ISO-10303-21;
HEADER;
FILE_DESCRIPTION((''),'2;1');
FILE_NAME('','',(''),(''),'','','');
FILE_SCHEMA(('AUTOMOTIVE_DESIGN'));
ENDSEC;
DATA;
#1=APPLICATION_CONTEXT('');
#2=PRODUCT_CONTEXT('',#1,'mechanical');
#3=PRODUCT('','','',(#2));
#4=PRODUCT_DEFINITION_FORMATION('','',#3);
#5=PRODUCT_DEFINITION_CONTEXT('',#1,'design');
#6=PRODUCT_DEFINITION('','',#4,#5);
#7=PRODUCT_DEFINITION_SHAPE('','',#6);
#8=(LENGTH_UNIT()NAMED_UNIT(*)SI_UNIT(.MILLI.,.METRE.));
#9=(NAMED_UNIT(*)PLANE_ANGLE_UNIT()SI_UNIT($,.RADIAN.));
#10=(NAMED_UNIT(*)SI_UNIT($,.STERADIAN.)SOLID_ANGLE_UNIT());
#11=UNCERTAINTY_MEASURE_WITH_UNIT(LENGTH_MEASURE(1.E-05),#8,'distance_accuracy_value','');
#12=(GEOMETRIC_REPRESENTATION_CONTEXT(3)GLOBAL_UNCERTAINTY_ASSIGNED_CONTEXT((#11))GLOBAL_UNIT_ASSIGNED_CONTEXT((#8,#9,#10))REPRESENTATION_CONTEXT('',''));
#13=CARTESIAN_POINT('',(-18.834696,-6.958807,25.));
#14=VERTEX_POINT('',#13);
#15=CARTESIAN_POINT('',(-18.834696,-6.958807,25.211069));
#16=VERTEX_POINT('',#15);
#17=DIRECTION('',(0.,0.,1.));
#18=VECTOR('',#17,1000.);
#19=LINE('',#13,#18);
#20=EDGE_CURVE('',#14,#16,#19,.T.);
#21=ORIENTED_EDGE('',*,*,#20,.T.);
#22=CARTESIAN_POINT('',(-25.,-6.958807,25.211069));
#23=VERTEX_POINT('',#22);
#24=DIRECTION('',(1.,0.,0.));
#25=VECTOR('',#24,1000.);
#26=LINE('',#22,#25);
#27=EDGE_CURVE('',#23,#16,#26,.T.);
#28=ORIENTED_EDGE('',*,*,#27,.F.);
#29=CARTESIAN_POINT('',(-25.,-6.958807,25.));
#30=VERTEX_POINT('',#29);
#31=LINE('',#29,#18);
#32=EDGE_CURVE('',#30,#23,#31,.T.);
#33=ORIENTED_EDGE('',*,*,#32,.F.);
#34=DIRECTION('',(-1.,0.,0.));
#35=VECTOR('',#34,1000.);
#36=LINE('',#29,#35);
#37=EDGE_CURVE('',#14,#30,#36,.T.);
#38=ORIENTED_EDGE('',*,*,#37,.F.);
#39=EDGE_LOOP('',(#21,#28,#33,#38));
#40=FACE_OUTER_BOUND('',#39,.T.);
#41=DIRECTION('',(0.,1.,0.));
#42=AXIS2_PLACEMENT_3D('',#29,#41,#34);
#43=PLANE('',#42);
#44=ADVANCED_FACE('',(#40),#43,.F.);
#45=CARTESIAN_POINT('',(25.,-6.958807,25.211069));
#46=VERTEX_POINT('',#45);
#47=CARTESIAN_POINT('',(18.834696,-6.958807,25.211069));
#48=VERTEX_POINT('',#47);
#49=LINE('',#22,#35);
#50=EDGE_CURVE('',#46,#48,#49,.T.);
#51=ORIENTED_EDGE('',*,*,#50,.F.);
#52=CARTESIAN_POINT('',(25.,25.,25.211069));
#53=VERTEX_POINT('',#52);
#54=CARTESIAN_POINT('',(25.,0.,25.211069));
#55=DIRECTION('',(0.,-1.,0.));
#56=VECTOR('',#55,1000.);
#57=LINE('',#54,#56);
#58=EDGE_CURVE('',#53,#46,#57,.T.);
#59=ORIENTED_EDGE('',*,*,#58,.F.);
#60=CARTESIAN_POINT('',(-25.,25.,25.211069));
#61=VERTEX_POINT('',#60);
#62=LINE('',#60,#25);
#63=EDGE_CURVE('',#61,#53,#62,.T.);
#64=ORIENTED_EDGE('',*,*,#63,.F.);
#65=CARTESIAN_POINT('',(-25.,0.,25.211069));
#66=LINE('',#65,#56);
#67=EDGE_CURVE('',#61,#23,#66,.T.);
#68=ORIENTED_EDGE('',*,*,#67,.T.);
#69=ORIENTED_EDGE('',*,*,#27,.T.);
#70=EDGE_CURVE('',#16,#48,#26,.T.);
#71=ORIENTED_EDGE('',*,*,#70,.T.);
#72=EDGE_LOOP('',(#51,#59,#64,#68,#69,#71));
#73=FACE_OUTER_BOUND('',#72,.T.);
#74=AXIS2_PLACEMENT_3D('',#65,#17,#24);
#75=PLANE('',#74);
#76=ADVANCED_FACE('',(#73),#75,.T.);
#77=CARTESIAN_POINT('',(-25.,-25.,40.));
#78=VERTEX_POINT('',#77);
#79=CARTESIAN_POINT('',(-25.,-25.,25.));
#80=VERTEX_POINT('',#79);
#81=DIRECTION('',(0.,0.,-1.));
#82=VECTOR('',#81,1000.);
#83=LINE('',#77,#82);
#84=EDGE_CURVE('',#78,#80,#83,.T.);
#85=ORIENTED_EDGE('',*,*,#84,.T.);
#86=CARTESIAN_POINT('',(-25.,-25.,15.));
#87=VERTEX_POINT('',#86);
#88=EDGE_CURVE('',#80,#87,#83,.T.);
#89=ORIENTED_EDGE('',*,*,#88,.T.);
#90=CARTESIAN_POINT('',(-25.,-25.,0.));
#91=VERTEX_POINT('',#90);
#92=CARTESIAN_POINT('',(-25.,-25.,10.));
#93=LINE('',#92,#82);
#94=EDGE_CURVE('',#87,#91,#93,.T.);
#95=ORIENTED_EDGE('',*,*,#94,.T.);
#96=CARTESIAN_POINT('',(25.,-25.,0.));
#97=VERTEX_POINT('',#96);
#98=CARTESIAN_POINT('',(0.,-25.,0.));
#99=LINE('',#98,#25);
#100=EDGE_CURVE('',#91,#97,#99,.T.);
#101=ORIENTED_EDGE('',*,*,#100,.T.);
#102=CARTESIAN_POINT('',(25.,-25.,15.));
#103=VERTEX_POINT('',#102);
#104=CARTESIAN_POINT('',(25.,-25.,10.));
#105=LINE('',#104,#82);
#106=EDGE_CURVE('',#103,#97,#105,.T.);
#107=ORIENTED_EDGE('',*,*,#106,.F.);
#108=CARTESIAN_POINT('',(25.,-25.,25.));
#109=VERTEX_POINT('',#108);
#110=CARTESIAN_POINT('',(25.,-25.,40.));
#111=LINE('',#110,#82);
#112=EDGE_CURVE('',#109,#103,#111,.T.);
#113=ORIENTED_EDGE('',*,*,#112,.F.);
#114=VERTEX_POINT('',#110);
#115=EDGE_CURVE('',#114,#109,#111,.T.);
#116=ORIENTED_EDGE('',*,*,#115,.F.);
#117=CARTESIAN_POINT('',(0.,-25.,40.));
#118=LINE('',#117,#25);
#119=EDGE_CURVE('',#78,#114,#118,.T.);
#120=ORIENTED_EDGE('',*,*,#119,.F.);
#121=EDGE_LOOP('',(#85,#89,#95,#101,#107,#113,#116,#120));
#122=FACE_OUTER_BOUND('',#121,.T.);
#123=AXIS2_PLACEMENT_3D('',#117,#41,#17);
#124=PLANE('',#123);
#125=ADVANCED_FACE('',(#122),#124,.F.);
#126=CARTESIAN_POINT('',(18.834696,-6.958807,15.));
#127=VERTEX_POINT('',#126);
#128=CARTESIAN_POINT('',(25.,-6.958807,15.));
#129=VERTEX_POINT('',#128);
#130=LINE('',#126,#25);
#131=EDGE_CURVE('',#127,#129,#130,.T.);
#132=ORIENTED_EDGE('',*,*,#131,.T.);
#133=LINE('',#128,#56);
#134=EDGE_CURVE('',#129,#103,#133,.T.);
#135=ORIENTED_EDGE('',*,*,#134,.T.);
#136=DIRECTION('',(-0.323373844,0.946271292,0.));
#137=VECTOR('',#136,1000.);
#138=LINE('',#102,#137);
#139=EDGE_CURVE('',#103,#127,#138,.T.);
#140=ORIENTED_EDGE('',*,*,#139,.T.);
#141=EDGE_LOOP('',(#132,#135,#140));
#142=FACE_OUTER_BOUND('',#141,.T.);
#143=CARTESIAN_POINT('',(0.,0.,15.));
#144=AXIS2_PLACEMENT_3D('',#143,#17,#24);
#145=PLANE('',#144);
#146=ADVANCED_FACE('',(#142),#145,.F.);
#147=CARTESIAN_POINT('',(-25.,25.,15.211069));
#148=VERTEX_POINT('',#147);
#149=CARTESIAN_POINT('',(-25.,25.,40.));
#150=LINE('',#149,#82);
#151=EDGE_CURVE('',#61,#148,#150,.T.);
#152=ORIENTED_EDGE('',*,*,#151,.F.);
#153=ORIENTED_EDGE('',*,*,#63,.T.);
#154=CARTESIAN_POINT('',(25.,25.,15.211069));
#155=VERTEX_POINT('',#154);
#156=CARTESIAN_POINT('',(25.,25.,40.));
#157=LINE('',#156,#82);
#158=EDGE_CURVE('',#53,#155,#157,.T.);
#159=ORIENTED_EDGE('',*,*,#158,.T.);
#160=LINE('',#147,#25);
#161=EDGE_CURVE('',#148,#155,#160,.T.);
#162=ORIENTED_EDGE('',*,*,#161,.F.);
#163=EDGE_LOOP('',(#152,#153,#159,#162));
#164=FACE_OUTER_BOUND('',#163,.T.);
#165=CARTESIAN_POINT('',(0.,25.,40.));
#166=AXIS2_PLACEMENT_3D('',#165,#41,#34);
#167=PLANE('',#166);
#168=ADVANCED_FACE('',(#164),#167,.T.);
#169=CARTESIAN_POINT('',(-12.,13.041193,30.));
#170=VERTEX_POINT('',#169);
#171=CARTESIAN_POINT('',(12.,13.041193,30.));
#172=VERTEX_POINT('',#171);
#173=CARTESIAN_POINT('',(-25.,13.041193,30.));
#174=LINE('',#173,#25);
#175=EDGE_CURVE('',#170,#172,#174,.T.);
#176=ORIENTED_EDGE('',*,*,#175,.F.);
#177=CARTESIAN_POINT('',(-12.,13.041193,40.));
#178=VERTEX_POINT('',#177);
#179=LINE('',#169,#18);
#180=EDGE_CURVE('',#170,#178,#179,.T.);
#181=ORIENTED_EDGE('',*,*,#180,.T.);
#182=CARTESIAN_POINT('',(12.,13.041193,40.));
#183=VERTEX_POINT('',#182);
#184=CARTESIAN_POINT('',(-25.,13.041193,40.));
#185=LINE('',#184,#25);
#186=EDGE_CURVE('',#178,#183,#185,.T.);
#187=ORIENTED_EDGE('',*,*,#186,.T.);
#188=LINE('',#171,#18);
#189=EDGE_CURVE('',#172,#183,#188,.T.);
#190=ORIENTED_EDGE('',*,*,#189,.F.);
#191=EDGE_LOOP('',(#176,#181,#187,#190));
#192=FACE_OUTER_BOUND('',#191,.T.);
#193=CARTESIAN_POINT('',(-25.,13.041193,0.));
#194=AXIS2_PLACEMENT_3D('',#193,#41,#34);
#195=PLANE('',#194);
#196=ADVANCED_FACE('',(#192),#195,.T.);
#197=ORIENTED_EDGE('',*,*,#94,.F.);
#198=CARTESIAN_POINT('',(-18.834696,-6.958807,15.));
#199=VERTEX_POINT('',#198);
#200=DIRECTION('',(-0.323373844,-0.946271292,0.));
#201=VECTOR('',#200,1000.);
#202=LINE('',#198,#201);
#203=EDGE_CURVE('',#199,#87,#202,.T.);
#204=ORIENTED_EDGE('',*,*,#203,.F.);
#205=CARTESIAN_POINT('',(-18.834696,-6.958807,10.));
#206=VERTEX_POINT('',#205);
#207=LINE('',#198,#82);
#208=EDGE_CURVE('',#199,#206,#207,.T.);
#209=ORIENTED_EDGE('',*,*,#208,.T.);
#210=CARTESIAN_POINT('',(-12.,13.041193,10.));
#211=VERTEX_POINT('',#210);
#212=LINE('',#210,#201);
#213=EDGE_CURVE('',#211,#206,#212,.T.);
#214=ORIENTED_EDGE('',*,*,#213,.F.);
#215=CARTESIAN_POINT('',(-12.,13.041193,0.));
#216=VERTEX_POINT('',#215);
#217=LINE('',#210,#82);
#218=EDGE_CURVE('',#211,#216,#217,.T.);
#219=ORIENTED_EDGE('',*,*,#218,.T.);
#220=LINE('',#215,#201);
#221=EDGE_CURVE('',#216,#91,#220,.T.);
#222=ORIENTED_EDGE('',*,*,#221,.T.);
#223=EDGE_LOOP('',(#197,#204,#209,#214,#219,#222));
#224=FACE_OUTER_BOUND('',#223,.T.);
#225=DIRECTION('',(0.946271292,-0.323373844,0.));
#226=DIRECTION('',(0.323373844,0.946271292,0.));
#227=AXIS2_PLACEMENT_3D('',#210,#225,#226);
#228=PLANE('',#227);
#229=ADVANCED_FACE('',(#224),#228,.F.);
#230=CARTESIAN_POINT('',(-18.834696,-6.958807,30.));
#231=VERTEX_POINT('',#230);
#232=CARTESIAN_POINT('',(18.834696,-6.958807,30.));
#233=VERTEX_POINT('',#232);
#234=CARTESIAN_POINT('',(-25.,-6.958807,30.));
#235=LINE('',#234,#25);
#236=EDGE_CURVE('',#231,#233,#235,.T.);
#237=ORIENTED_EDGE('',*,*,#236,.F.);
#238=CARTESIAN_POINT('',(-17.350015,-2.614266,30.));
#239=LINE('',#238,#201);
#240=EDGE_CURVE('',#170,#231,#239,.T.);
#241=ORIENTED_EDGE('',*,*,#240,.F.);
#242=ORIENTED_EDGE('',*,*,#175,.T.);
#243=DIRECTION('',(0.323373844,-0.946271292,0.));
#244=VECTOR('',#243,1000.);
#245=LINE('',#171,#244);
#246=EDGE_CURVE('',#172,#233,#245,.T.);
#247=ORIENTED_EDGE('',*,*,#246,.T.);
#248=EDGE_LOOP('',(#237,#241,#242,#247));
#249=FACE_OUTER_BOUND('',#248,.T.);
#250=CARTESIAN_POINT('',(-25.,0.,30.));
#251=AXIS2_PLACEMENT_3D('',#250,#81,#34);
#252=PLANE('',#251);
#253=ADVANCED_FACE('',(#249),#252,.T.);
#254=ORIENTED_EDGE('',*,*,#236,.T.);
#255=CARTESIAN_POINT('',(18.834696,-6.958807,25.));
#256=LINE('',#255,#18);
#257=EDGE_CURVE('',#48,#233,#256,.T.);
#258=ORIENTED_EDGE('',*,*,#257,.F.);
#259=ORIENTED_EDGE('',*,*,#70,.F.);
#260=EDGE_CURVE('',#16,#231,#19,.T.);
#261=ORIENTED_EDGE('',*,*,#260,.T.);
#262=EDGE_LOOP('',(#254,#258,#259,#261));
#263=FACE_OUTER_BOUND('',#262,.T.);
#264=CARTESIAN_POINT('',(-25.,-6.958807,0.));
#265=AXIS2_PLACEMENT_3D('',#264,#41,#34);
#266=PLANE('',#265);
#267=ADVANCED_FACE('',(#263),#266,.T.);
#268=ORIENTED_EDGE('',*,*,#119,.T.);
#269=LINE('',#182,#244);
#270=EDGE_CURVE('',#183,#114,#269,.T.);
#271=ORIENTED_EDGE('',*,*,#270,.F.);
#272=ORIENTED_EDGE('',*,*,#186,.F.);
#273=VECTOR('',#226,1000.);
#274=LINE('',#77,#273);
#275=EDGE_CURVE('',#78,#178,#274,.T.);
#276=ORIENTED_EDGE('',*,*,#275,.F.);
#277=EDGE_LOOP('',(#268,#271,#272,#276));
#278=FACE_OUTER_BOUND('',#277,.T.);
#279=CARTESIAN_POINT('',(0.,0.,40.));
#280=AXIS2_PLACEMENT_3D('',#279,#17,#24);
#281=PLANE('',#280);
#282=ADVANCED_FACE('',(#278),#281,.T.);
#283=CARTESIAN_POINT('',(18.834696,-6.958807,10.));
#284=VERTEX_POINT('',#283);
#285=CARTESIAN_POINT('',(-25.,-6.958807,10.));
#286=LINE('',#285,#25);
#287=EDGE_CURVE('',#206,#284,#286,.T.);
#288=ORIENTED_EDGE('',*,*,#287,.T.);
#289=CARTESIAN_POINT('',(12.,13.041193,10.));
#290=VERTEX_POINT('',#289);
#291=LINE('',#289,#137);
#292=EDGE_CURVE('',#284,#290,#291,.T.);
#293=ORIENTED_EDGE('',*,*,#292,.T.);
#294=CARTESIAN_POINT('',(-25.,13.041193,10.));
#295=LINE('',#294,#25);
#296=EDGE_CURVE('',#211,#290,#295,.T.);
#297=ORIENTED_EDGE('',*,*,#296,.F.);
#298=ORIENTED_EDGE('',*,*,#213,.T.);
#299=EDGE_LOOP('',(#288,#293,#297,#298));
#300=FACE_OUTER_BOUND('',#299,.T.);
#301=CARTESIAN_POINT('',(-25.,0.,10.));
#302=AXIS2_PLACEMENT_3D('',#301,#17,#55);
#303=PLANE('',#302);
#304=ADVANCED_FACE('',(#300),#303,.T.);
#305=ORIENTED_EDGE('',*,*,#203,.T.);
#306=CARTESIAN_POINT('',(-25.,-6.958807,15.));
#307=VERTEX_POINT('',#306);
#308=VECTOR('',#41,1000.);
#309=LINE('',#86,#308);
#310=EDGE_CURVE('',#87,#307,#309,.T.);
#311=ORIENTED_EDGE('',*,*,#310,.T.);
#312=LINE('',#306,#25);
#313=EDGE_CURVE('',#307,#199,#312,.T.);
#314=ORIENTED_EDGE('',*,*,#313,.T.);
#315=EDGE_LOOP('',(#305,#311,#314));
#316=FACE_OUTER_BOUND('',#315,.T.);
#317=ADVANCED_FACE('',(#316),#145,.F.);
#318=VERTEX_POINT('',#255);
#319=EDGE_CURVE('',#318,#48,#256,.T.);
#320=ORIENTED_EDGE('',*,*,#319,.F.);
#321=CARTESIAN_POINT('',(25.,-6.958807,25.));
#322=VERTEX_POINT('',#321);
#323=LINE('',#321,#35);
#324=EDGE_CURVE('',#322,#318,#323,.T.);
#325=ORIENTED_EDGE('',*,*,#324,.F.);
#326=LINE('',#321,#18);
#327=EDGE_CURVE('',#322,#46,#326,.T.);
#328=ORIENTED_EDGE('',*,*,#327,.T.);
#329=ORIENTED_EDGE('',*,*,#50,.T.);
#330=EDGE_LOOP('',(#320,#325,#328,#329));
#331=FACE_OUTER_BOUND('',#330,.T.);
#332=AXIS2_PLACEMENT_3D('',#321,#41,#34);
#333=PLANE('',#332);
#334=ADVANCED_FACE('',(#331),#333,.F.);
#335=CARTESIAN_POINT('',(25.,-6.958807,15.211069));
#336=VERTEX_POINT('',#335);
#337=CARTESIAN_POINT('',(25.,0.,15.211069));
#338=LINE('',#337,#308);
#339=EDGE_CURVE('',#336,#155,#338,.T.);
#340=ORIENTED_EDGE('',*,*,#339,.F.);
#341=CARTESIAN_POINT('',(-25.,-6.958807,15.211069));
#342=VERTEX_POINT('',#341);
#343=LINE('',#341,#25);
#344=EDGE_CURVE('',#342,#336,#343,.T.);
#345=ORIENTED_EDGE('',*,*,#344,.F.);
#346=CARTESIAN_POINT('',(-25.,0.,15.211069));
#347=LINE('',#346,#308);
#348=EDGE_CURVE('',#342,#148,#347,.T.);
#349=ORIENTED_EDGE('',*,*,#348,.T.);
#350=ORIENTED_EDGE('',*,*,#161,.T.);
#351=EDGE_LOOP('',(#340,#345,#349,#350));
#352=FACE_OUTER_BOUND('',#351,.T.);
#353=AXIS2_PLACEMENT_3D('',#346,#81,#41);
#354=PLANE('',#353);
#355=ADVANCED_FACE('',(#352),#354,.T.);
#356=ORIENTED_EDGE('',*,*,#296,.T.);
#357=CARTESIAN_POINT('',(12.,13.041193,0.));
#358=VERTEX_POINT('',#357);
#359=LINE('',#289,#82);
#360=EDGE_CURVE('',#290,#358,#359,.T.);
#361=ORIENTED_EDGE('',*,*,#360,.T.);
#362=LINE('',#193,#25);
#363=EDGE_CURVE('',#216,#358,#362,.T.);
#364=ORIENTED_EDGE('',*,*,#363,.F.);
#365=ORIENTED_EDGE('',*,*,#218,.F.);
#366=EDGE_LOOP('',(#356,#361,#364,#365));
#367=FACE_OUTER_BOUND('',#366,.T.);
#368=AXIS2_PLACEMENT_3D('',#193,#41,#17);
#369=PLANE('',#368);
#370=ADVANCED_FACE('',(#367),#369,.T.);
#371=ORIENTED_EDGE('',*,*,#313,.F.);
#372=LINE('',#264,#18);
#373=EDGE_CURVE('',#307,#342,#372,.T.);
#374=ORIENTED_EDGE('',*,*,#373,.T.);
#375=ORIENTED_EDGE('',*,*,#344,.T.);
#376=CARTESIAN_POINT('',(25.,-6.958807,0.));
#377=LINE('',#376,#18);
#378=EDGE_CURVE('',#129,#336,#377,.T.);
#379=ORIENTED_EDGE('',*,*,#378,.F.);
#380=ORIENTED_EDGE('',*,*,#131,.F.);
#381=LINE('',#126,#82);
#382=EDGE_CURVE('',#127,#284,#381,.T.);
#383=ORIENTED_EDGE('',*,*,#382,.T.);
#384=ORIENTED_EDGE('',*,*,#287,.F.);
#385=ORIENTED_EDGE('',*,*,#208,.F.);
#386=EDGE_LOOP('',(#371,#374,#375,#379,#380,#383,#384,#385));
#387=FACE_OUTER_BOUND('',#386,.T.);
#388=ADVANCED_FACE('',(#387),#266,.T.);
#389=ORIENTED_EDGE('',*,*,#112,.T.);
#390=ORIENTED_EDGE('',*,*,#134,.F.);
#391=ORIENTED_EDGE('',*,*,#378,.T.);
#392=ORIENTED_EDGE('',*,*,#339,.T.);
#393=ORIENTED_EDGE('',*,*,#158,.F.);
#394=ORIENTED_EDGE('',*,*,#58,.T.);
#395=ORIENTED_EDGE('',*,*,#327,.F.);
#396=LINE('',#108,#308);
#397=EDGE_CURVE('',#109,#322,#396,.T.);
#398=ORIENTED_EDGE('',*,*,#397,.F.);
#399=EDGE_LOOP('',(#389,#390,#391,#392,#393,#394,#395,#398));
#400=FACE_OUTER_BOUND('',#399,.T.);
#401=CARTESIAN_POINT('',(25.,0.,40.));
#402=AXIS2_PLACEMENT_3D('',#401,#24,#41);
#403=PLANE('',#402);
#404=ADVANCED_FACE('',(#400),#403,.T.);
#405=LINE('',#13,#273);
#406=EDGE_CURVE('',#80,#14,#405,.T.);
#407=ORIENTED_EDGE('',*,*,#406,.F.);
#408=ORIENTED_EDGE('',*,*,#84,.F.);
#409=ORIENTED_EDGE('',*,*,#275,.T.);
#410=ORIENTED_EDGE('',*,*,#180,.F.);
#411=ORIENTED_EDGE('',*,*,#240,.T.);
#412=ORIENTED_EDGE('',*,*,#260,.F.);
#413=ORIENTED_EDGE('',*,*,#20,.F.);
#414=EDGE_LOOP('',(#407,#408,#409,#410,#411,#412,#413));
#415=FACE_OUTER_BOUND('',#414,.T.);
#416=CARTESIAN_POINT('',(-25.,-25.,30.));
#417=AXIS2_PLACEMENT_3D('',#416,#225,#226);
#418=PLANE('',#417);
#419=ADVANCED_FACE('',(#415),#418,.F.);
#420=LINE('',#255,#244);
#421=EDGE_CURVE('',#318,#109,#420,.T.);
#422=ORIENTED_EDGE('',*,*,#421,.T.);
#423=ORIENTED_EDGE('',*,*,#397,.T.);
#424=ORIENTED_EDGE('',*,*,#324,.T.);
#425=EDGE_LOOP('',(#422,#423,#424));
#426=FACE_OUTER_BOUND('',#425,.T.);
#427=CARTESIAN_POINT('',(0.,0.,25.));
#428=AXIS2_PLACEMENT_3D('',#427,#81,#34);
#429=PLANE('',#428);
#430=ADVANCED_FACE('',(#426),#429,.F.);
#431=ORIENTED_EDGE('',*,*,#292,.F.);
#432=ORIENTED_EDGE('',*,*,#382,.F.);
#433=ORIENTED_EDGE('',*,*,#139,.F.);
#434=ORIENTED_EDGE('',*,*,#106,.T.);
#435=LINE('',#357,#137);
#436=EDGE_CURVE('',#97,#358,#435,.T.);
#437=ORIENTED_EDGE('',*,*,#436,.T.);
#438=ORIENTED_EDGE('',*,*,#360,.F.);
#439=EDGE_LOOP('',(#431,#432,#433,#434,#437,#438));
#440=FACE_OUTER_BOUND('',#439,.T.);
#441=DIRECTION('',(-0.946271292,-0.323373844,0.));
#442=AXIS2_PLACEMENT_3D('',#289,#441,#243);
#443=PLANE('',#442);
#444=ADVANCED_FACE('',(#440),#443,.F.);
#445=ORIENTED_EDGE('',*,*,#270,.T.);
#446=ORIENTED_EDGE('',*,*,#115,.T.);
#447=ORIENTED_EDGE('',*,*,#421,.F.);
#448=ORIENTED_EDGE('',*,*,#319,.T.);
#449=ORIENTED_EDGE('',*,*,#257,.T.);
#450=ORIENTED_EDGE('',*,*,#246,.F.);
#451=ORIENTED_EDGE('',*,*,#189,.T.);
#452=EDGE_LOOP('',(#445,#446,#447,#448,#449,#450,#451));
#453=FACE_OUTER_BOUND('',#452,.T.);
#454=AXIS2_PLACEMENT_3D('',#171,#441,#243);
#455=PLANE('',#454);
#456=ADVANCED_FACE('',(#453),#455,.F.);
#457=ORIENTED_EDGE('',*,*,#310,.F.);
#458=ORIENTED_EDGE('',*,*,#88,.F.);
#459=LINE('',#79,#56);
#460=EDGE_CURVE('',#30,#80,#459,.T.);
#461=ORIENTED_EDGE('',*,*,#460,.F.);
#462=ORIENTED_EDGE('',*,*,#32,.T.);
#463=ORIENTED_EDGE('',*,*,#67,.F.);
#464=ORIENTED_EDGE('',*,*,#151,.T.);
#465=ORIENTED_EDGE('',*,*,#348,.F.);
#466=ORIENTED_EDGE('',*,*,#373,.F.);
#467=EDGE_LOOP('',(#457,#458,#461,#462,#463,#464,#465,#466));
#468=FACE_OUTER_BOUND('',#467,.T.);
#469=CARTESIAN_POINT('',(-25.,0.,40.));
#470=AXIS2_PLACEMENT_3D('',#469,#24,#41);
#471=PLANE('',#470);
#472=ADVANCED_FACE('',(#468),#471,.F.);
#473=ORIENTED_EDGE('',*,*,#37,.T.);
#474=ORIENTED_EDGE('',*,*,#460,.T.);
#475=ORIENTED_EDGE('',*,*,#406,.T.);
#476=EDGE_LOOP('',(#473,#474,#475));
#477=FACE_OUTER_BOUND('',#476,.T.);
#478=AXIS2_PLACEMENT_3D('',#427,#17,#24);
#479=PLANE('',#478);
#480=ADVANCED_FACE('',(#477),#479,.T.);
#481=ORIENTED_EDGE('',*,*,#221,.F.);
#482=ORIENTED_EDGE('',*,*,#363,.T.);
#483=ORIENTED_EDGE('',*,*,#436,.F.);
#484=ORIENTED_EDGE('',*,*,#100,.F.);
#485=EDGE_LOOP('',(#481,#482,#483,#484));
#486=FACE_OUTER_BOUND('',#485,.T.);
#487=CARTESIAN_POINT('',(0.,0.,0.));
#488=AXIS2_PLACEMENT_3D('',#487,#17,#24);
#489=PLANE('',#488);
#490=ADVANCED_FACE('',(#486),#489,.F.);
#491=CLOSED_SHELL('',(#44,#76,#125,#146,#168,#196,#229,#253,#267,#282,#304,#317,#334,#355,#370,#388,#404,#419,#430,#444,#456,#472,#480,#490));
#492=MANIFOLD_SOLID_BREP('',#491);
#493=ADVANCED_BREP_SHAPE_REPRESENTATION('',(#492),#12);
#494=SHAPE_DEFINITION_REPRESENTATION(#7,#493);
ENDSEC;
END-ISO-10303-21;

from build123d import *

# Parameters (mm, degrees)
BASE_BLOCK_40MM_DEPTH       = 40
STEP_PROFILE_CUT_SKETCH_W   = 10
STEP_PROFILE_CUT_SKETCH_H   = 11.958807021
STEP_PROFILE_CUT_DEPTH      = 69.738635424
POCKET_24MM_X_10_DEEP_DEPTH = 10
POCKET_12MM_X_10_DEEP_DEPTH = 10
TRIANGULAR_CUT_A_5MM_DEPTH  = 5
TRIANGULAR_CUT_B_5MM_DEPTH  = 5
TRIANGULAR_CUT_C_5MM_DEPTH  = 5
TRIANGULAR_CUT_D_5MM_DEPTH  = 5


with BuildPart() as part:
    # Base Profile Sketch → Base Block 40mm (new body)
    with BuildSketch(Plane.XY):
        Polygon((12, 25), (-12, 25), (-25, 25), (-25, -25), (-12, 13), (12, 13), (25, -25), (25, 25), align=None)
        Polygon((12, 13), (25, -25), (-25, -25), (-12, 13), align=None)
    extrude(amount=BASE_BLOCK_40MM_DEPTH)

    # Step Profile Cut Sketch → Step Profile Cut (cut, through all)
    with BuildSketch(Plane(origin=(25, 0, 0), x_dir=(0, 0, -1), z_dir=(1, 0, 0))):
        Polygon((-25.21106926, -6.958807021), (-25.21106926, 25), (-30, 25), (-40, 25), (-40, 13.041192979), (-30, 13.041192979), (-30, -6.958807021), align=None)
        Polygon((-10, -6.958807021), (-10, 13.041192979), (-10, 25), (-15.21106926, 25), (-15.21106926, -6.958807021), align=None)
        with Locations((-5, 19.02059649)):
            Rectangle(STEP_PROFILE_CUT_SKETCH_W, STEP_PROFILE_CUT_SKETCH_H)
    extrude(amount=-STEP_PROFILE_CUT_DEPTH, mode=Mode.SUBTRACT)

    # Pocket 24mm Sketch → Pocket 24mm x 10 Deep (cut)
    with BuildSketch(Plane(origin=(0, 0, 0), x_dir=(-1, 0, 0), z_dir=(0, 0, -1))):
        Polygon((-12, 13.041192979), (12, 13.041192979), (25, -25), (25, 25), (-25, 25), (-25, -25), align=None)
    extrude(amount=-POCKET_24MM_X_10_DEEP_DEPTH, mode=Mode.SUBTRACT)

    # Pocket 12mm Sketch → Pocket 12mm x 10 Deep (cut)
    with BuildSketch(Plane.XY.offset(40)):
        Polygon((-25, -25), (-12, 13.041192979), (12, 13.041192979), (25, -25), (25, 25), (-25, 25), align=None)
    extrude(amount=-POCKET_12MM_X_10_DEEP_DEPTH, mode=Mode.SUBTRACT)

    # Triangular Cut A Sketch → Triangular Cut A 5mm (cut)
    with BuildSketch(Plane.XY.offset(30)):
        Polygon((-25, -25), (-25, -6.958807021), (-18.834696276, -6.958807021), align=None)
    extrude(amount=-TRIANGULAR_CUT_A_5MM_DEPTH, mode=Mode.SUBTRACT)

    # Triangular Cut B Sketch → Triangular Cut B 5mm (cut)
    with BuildSketch(Plane(origin=(0, 0, 10), x_dir=(-1, 0, 0), z_dir=(0, 0, -1))):
        Polygon((25, -25), (25, -6.958807021), (18.834696276, -6.958807021), align=None)
    extrude(amount=-TRIANGULAR_CUT_B_5MM_DEPTH, mode=Mode.SUBTRACT)

    # Triangular Cut C Sketch → Triangular Cut C 5mm (cut)
    with BuildSketch(Plane(origin=(0, 0, 10), x_dir=(-1, 0, 0), z_dir=(0, 0, -1))):
        Polygon((-25, -25), (-18.834696276, -6.958807021), (-25, -6.958807021), align=None)
    extrude(amount=-TRIANGULAR_CUT_C_5MM_DEPTH, mode=Mode.SUBTRACT)

    # Triangular Cut D Sketch → Triangular Cut D 5mm (cut)
    with BuildSketch(Plane.XY.offset(30)):
        Polygon((25, -25), (25, -6.958807021), (18.834696276, -6.958807021), align=None)
    extrude(amount=-TRIANGULAR_CUT_D_5MM_DEPTH, mode=Mode.SUBTRACT)


solid = part.part
